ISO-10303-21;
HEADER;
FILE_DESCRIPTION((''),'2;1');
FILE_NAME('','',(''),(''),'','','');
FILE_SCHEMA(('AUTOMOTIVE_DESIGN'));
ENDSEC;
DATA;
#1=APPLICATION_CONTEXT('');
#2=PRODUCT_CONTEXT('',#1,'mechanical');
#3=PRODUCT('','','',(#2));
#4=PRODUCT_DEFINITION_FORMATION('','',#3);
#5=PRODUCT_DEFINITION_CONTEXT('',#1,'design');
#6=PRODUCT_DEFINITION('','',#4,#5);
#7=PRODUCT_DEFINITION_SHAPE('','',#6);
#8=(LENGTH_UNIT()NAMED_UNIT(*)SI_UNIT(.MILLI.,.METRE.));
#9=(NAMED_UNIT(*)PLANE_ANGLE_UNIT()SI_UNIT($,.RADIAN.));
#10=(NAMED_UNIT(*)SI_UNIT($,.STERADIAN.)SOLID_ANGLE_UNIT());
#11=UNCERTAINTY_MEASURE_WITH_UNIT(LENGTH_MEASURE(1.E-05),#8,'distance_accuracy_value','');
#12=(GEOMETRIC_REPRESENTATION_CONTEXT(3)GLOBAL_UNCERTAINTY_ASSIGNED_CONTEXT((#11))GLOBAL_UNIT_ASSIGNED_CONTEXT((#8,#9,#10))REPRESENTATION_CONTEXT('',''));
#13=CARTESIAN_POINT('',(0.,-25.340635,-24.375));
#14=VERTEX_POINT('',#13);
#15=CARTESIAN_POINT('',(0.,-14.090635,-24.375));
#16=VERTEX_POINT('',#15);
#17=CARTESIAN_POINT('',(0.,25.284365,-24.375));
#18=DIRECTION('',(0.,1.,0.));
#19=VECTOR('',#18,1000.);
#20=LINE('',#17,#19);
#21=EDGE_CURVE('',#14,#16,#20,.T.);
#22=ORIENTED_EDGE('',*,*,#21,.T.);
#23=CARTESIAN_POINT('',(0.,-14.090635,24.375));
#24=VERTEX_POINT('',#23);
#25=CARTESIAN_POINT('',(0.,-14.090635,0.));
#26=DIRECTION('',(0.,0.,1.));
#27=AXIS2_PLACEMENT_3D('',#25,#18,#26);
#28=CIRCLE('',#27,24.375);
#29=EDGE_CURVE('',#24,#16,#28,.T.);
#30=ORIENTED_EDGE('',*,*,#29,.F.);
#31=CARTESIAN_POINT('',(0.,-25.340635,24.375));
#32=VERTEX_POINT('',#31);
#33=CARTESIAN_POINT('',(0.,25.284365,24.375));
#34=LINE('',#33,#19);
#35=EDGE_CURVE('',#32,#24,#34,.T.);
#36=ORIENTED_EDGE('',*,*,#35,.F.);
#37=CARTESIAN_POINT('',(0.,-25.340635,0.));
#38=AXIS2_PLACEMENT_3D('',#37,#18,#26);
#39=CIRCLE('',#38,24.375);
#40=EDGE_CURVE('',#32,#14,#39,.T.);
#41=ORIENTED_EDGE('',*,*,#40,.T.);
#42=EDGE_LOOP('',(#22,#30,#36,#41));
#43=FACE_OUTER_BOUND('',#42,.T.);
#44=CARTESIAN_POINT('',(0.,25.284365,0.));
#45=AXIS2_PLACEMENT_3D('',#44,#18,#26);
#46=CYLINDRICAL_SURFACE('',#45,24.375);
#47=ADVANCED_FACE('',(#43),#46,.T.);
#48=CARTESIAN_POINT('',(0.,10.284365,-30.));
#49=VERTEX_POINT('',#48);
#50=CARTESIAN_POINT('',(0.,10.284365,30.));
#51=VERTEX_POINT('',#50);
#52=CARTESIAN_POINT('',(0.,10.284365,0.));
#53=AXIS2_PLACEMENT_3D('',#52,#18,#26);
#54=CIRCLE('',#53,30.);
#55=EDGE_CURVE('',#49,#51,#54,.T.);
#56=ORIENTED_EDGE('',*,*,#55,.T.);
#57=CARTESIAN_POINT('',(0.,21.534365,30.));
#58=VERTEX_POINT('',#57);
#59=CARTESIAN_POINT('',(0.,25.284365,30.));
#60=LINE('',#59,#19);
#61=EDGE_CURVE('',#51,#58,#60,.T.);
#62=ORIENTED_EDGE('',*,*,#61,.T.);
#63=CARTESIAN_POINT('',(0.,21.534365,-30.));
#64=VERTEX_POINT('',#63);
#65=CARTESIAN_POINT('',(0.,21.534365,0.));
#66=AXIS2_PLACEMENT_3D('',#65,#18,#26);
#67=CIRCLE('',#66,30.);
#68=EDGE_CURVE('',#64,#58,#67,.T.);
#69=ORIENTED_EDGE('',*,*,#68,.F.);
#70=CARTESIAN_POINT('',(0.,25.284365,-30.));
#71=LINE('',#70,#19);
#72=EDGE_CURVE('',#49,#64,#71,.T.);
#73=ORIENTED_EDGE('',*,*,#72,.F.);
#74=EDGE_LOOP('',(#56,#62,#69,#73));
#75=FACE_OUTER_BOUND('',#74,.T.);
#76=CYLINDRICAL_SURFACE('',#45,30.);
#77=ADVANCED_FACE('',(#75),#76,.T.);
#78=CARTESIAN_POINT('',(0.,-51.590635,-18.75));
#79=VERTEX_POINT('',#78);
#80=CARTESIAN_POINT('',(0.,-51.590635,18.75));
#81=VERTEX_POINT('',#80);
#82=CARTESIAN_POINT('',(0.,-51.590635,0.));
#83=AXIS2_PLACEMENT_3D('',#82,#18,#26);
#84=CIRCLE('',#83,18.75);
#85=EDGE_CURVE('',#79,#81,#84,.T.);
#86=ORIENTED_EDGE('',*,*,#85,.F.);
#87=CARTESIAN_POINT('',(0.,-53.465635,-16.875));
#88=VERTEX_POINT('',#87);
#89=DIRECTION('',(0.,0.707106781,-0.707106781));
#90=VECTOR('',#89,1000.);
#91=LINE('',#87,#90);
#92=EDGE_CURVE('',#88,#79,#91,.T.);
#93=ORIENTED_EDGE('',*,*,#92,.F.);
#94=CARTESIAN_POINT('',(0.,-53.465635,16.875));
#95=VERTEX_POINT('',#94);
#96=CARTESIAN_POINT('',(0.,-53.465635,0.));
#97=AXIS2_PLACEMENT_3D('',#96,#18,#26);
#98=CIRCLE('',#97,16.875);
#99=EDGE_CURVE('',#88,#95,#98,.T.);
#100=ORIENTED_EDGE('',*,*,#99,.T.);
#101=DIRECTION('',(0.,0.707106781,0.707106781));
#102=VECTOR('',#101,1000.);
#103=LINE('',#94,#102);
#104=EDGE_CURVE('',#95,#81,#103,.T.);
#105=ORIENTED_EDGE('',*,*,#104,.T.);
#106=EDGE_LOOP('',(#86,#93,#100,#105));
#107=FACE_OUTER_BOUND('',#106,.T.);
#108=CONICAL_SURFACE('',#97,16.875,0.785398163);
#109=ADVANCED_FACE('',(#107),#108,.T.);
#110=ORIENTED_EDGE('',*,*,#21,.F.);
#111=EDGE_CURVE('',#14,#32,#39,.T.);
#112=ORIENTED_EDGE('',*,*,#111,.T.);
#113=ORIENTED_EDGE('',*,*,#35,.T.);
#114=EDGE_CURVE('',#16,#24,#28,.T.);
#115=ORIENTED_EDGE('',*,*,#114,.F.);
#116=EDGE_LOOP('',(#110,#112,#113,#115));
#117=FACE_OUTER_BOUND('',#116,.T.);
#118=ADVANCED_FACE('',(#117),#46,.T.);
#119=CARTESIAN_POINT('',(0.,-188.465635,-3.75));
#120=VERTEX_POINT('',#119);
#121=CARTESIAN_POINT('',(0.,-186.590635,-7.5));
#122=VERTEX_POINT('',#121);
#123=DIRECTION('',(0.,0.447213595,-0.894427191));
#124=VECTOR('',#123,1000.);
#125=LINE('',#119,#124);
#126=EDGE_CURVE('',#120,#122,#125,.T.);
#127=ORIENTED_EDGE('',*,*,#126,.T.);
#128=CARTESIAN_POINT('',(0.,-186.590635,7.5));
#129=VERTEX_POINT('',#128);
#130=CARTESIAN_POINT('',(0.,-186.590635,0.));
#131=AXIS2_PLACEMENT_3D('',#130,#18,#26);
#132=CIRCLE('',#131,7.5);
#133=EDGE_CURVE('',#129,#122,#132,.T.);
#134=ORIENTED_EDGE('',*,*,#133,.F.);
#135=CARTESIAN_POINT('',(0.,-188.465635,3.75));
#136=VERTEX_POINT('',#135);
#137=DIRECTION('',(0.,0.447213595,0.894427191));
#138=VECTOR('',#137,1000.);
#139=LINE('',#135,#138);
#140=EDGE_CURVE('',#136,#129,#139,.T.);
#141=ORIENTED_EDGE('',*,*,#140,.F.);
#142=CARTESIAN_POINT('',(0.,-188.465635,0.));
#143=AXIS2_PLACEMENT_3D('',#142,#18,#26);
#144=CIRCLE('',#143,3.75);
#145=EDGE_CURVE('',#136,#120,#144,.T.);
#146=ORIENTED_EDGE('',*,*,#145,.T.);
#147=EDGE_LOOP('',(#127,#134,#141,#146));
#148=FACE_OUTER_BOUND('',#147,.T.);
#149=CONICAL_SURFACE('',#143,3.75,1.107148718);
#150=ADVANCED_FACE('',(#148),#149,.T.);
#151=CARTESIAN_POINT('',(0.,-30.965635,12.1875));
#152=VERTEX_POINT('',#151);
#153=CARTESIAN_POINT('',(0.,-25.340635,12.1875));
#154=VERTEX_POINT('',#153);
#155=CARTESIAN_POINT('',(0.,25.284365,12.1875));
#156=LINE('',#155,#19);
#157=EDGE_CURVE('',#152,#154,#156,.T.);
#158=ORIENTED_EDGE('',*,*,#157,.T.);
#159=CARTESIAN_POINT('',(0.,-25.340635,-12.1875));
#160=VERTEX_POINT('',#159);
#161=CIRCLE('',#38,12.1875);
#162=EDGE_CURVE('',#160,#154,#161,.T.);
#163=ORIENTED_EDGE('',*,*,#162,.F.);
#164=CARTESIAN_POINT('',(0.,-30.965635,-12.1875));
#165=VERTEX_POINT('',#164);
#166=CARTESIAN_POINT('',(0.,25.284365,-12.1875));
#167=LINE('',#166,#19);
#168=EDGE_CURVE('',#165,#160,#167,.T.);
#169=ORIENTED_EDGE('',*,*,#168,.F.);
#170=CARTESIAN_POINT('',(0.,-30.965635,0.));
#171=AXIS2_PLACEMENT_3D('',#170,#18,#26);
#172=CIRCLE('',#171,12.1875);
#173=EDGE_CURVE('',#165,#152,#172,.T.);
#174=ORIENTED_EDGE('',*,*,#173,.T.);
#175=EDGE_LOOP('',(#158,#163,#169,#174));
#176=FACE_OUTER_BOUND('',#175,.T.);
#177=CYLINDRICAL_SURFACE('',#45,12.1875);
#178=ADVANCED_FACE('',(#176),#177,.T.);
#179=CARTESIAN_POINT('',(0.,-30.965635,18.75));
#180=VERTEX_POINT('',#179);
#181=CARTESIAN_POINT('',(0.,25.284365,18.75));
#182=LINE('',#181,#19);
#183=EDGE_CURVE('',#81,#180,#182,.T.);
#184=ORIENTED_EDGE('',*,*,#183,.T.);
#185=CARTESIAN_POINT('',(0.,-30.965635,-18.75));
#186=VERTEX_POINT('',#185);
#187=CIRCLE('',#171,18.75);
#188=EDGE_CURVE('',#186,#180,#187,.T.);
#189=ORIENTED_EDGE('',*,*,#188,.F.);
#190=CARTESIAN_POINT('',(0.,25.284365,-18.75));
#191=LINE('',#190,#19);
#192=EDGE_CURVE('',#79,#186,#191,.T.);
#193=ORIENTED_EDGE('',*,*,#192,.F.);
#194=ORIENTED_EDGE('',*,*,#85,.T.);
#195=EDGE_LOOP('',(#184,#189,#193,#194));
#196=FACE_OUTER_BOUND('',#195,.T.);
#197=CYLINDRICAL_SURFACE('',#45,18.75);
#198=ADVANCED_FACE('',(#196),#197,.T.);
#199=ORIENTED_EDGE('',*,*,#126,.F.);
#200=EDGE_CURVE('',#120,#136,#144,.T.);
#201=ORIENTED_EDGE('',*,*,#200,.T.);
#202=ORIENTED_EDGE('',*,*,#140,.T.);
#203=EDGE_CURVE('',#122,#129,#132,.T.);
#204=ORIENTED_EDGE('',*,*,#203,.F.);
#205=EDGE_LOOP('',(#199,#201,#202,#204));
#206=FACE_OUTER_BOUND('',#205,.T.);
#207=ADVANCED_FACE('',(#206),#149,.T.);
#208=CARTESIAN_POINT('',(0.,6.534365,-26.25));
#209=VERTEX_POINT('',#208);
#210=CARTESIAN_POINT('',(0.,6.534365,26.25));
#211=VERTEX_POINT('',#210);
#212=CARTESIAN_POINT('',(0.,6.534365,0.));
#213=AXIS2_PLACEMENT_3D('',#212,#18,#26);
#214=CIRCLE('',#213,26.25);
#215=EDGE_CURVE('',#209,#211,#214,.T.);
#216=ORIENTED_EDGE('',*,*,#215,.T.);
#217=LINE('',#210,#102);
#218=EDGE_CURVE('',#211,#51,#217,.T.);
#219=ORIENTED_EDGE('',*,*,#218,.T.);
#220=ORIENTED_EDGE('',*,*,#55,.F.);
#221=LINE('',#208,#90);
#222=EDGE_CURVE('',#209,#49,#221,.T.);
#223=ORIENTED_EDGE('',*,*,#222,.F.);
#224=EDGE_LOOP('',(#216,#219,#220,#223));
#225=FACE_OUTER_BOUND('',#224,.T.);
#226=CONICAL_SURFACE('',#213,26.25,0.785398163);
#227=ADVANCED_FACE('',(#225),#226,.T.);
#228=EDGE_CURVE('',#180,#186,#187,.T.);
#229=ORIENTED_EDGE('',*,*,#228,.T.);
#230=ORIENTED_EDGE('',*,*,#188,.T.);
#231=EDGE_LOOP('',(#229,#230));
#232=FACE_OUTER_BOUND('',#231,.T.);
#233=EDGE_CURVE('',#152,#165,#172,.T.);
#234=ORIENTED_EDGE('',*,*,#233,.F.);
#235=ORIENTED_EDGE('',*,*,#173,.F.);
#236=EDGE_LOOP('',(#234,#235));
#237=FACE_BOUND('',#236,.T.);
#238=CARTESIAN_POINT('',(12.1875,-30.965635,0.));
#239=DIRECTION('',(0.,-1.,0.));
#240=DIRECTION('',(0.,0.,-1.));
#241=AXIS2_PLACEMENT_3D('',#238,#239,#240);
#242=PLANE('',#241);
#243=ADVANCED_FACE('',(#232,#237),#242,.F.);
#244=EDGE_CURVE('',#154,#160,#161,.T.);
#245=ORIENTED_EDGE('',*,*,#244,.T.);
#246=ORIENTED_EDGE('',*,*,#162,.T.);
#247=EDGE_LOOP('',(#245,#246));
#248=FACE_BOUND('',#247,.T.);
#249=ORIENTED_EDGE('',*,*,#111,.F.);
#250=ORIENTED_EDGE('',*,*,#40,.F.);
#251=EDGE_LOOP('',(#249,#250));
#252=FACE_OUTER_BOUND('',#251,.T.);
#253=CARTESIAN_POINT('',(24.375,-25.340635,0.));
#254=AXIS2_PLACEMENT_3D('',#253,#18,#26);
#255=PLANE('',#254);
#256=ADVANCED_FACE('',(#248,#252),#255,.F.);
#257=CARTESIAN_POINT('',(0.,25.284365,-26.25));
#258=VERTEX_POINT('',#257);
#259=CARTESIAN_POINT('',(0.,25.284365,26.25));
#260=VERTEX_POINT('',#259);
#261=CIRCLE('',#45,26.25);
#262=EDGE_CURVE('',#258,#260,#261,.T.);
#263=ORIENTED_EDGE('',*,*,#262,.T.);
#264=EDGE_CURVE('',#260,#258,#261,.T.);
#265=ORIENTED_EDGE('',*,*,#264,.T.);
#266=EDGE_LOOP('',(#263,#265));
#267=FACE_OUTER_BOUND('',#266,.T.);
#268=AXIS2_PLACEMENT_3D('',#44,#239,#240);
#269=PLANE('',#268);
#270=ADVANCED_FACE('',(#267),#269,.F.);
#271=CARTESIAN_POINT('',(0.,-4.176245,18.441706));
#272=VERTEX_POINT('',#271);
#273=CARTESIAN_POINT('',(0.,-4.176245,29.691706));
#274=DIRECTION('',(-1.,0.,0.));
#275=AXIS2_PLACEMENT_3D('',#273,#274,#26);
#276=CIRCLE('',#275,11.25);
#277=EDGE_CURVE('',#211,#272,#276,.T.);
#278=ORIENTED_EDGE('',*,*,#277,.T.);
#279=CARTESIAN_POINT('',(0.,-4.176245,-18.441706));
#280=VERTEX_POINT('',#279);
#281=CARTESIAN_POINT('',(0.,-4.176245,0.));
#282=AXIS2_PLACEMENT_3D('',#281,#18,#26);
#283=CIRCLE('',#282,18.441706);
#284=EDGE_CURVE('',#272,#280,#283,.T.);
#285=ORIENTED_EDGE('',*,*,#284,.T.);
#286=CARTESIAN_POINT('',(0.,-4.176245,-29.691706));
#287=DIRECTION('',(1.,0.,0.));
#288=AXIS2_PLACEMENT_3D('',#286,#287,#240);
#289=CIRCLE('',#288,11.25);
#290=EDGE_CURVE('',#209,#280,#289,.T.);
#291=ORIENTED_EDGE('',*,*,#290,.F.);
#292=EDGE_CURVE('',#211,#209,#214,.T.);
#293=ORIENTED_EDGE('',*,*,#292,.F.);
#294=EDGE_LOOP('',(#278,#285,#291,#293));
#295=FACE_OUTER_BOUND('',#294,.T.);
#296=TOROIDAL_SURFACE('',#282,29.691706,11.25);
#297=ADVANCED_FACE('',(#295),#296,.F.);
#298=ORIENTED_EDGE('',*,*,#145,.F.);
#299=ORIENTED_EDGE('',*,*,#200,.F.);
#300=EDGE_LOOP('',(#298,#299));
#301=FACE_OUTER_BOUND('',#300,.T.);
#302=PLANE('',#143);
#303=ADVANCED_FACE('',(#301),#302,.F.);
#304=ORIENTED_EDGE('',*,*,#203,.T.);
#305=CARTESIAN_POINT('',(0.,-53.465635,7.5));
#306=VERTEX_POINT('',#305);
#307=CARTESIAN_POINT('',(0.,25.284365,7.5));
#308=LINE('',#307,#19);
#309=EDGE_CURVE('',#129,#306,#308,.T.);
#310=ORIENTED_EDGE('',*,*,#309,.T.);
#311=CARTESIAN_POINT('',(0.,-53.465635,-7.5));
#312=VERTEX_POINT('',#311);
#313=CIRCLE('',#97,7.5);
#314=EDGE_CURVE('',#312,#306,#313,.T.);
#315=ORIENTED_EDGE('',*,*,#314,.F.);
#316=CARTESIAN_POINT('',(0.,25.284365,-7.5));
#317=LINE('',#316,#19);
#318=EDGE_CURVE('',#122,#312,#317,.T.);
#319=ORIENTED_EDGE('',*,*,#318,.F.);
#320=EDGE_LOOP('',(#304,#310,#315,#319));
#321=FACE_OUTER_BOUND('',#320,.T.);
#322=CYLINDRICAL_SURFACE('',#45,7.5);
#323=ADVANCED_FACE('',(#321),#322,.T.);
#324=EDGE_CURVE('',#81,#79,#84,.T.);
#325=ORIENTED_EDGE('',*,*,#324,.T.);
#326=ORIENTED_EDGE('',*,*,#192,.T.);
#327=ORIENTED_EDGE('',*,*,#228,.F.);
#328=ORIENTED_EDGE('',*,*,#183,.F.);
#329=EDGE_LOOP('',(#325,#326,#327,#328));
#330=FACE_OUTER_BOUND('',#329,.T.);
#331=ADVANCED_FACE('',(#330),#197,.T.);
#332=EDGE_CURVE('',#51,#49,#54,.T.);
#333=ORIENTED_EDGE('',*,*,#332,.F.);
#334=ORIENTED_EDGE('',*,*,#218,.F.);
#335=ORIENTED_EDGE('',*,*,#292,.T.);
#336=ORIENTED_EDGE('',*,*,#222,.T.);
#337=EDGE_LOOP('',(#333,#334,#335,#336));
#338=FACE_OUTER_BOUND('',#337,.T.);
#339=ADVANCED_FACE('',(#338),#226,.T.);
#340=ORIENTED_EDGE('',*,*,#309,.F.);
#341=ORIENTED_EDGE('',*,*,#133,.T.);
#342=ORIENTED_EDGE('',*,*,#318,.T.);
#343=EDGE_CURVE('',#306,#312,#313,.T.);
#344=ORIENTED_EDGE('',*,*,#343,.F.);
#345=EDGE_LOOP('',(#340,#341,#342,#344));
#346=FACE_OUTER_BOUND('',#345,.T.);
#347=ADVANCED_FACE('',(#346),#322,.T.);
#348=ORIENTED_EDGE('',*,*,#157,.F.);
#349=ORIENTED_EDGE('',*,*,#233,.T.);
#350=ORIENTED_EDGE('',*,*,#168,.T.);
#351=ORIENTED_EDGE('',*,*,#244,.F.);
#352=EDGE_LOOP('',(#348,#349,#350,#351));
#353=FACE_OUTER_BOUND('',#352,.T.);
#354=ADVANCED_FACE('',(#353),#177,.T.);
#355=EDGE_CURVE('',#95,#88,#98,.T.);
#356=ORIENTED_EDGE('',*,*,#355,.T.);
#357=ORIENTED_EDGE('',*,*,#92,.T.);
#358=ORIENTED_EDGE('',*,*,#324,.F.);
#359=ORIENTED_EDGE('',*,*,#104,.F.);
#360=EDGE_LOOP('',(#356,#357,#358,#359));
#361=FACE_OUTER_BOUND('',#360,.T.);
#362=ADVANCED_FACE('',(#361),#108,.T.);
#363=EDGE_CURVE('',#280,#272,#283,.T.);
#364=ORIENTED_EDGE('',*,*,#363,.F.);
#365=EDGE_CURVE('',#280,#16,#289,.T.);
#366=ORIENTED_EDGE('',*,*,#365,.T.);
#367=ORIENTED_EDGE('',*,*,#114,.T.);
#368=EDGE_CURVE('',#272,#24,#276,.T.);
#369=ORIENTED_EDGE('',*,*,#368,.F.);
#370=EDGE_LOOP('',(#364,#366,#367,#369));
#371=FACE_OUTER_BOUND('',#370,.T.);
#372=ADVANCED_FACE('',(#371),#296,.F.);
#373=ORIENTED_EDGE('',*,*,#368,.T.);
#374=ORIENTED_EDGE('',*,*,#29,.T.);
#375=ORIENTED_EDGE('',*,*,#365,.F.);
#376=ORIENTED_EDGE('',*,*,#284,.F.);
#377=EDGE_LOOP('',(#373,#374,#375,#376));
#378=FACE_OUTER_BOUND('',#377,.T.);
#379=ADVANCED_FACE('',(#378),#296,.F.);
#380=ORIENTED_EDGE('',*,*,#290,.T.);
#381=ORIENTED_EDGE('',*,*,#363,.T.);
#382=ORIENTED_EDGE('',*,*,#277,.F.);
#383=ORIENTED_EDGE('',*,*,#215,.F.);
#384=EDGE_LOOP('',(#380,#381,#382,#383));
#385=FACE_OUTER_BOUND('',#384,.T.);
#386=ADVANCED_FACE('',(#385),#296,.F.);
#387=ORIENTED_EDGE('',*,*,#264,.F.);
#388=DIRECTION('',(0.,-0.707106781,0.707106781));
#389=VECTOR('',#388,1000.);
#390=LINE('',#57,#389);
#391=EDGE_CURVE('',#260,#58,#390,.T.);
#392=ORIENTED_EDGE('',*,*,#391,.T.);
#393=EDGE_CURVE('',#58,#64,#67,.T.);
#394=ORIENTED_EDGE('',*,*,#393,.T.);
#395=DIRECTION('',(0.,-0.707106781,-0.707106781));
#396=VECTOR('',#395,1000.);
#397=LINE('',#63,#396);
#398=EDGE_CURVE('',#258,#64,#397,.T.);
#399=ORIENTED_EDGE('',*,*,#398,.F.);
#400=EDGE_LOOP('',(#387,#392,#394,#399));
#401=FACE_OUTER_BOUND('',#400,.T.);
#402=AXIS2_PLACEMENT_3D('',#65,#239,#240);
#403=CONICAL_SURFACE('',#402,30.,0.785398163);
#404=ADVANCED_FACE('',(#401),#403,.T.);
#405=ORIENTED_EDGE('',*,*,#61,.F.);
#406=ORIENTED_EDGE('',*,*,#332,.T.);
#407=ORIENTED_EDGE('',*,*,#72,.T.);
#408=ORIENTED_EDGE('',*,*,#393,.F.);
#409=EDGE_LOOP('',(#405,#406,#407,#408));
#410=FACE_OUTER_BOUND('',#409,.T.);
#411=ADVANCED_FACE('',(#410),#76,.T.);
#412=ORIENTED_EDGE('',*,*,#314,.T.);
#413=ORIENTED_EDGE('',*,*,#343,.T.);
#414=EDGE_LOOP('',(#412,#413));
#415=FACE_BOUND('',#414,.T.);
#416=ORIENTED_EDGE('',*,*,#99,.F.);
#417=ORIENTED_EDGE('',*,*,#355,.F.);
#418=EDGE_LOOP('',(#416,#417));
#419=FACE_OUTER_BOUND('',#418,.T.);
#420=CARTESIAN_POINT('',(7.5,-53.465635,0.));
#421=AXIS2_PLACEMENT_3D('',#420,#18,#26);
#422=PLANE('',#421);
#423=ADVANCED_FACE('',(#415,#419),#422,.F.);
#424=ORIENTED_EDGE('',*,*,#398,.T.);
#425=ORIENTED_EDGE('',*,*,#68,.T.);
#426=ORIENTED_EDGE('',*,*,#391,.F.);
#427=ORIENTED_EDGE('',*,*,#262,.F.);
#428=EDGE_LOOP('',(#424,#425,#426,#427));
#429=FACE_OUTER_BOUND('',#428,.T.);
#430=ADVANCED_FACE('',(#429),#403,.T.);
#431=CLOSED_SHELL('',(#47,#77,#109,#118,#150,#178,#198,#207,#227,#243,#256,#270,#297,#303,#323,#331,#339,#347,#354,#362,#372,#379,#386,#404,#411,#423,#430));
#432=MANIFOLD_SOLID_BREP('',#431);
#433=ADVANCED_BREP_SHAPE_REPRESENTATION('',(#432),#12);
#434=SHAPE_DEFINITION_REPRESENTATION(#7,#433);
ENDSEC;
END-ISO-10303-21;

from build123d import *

# Parameters (mm, degrees)
SCALE_1_SCALE = 1.875


with BuildPart() as part:
    # Sketch1 → Revolve1 (revolve)
    with BuildSketch(Plane.XY, mode=Mode.PRIVATE) as revolve1_sk:
        with BuildLine():
            Line((4, -40), (4, -111))
            Line((4, -111), (2, -112))
            Line((2, -112), (0, -112))
            Line((0, -112), (0, 2))
            Line((0, 2), (14, 2))
            Line((14, 2), (16, 0))
            Line((16, 0), (16, -6))
            Line((16, -6), (14, -8))
            ThreePointArc((14, -8), (9.860217357, -13.169110669), (13, -19))
            Line((13, -19), (13, -25))
            Line((13, -25), (6.5, -25))
            Line((6.5, -25), (6.5, -28))
            Line((6.5, -28), (10, -28))
            Line((10, -28), (10, -39))
            Line((10, -39), (9, -40))
            Line((9, -40), (4, -40))
        make_face()
    revolve(revolve1_sk.sketch.rotate(Axis((0, 2, 0), (0, -1, 0)), 90), axis=Axis((0, 2, 0), (0, -1, 0)))


with BuildPart() as part_1:
    # Scale 1: scaled about (0, -24.610702711, 0)
    add(part.part.scale(SCALE_1_SCALE).moved(Location((0, 21.534364872, 0))))


solid = part_1.part
